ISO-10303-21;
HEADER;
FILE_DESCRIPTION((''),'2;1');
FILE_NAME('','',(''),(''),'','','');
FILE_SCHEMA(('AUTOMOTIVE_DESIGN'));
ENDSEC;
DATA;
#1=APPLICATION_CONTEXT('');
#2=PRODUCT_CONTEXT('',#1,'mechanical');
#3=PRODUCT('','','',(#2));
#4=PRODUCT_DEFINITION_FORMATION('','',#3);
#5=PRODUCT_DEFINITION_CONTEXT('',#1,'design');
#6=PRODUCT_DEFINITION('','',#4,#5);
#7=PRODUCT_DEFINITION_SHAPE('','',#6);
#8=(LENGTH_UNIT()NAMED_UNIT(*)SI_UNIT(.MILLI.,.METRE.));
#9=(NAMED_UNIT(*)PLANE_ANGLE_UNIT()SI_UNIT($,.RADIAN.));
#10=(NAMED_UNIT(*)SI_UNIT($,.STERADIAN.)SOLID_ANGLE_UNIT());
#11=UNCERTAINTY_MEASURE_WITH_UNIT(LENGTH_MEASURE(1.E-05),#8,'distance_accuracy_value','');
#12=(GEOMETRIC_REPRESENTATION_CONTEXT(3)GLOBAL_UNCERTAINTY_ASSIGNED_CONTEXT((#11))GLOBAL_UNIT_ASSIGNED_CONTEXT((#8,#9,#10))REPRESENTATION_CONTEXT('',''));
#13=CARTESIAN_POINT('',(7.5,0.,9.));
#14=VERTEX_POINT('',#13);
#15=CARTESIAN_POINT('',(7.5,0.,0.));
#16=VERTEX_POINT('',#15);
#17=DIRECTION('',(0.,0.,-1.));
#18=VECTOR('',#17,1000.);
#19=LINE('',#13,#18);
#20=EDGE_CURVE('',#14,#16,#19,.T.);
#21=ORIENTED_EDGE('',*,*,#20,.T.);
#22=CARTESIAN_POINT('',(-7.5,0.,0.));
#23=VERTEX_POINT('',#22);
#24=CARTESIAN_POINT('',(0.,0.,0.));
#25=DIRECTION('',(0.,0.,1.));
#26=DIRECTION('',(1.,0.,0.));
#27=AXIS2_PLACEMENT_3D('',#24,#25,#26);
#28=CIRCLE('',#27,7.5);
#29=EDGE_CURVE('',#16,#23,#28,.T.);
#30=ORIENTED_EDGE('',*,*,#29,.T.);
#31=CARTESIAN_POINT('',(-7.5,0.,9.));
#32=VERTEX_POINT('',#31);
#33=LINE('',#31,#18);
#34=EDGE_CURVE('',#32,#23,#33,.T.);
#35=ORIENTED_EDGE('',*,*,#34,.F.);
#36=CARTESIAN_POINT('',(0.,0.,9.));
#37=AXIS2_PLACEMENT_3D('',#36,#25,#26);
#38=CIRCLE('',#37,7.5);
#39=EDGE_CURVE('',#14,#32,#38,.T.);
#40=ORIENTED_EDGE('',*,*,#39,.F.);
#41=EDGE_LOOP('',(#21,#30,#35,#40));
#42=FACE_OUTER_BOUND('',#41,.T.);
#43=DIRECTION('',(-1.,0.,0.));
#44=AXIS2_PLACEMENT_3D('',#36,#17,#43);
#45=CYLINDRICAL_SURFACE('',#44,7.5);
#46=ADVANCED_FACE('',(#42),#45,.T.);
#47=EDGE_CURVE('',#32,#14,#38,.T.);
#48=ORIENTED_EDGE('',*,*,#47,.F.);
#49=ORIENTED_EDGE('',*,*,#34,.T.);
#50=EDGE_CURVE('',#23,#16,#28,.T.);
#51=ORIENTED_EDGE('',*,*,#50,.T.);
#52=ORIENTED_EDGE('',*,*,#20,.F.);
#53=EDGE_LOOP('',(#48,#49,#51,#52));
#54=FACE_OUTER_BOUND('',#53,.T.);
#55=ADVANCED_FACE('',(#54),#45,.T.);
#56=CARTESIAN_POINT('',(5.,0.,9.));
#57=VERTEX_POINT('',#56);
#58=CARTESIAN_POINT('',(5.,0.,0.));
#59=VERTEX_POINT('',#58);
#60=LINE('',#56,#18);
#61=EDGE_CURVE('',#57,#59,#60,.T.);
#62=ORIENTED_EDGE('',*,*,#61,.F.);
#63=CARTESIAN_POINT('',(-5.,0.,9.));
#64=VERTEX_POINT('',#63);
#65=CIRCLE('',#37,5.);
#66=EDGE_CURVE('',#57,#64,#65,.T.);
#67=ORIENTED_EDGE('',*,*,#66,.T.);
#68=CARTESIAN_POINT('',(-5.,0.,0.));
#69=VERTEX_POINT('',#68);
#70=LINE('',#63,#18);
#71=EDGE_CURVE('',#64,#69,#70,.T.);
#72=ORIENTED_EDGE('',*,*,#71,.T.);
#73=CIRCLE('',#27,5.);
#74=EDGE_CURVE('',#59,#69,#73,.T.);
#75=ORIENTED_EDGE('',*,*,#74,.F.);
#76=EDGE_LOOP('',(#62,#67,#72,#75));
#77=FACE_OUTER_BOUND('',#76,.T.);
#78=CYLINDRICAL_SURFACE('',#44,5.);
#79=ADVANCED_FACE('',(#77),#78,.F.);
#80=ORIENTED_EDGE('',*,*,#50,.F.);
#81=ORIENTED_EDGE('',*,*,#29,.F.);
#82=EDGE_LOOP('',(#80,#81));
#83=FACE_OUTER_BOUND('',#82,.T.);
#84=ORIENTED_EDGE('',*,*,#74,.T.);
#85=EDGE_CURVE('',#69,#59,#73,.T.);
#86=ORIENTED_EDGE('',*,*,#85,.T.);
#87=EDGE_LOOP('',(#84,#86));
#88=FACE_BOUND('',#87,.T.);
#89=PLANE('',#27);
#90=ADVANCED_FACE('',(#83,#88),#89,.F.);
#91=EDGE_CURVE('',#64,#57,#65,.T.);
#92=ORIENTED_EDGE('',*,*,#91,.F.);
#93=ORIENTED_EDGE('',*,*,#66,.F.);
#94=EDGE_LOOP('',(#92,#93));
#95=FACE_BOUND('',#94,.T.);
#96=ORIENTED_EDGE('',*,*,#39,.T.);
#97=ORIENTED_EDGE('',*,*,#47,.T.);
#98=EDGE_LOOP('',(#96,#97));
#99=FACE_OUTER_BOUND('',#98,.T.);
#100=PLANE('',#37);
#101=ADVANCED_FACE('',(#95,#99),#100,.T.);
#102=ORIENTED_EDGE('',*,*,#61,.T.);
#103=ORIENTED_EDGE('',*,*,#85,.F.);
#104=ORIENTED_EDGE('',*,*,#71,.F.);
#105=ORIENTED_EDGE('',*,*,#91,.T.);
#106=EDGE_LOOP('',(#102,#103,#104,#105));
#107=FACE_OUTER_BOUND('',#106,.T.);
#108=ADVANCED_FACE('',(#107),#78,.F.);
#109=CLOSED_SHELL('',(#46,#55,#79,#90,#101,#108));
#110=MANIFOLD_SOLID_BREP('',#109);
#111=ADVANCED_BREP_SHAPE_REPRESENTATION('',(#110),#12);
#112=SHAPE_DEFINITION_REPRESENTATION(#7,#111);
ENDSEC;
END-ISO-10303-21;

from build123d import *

# Parameters (mm, degrees)
SKETCH1_R           = 7.5
SKETCH1_R_2         = 5
BOSS_EXTRUDE1_DEPTH = 9


with BuildPart() as part:
    # Sketch1 → Boss-Extrude1 (new body)
    with BuildSketch(Plane.XY):
        Circle(SKETCH1_R)
        Circle(SKETCH1_R_2, mode=Mode.SUBTRACT)
    extrude(amount=BOSS_EXTRUDE1_DEPTH)


solid = part.part
